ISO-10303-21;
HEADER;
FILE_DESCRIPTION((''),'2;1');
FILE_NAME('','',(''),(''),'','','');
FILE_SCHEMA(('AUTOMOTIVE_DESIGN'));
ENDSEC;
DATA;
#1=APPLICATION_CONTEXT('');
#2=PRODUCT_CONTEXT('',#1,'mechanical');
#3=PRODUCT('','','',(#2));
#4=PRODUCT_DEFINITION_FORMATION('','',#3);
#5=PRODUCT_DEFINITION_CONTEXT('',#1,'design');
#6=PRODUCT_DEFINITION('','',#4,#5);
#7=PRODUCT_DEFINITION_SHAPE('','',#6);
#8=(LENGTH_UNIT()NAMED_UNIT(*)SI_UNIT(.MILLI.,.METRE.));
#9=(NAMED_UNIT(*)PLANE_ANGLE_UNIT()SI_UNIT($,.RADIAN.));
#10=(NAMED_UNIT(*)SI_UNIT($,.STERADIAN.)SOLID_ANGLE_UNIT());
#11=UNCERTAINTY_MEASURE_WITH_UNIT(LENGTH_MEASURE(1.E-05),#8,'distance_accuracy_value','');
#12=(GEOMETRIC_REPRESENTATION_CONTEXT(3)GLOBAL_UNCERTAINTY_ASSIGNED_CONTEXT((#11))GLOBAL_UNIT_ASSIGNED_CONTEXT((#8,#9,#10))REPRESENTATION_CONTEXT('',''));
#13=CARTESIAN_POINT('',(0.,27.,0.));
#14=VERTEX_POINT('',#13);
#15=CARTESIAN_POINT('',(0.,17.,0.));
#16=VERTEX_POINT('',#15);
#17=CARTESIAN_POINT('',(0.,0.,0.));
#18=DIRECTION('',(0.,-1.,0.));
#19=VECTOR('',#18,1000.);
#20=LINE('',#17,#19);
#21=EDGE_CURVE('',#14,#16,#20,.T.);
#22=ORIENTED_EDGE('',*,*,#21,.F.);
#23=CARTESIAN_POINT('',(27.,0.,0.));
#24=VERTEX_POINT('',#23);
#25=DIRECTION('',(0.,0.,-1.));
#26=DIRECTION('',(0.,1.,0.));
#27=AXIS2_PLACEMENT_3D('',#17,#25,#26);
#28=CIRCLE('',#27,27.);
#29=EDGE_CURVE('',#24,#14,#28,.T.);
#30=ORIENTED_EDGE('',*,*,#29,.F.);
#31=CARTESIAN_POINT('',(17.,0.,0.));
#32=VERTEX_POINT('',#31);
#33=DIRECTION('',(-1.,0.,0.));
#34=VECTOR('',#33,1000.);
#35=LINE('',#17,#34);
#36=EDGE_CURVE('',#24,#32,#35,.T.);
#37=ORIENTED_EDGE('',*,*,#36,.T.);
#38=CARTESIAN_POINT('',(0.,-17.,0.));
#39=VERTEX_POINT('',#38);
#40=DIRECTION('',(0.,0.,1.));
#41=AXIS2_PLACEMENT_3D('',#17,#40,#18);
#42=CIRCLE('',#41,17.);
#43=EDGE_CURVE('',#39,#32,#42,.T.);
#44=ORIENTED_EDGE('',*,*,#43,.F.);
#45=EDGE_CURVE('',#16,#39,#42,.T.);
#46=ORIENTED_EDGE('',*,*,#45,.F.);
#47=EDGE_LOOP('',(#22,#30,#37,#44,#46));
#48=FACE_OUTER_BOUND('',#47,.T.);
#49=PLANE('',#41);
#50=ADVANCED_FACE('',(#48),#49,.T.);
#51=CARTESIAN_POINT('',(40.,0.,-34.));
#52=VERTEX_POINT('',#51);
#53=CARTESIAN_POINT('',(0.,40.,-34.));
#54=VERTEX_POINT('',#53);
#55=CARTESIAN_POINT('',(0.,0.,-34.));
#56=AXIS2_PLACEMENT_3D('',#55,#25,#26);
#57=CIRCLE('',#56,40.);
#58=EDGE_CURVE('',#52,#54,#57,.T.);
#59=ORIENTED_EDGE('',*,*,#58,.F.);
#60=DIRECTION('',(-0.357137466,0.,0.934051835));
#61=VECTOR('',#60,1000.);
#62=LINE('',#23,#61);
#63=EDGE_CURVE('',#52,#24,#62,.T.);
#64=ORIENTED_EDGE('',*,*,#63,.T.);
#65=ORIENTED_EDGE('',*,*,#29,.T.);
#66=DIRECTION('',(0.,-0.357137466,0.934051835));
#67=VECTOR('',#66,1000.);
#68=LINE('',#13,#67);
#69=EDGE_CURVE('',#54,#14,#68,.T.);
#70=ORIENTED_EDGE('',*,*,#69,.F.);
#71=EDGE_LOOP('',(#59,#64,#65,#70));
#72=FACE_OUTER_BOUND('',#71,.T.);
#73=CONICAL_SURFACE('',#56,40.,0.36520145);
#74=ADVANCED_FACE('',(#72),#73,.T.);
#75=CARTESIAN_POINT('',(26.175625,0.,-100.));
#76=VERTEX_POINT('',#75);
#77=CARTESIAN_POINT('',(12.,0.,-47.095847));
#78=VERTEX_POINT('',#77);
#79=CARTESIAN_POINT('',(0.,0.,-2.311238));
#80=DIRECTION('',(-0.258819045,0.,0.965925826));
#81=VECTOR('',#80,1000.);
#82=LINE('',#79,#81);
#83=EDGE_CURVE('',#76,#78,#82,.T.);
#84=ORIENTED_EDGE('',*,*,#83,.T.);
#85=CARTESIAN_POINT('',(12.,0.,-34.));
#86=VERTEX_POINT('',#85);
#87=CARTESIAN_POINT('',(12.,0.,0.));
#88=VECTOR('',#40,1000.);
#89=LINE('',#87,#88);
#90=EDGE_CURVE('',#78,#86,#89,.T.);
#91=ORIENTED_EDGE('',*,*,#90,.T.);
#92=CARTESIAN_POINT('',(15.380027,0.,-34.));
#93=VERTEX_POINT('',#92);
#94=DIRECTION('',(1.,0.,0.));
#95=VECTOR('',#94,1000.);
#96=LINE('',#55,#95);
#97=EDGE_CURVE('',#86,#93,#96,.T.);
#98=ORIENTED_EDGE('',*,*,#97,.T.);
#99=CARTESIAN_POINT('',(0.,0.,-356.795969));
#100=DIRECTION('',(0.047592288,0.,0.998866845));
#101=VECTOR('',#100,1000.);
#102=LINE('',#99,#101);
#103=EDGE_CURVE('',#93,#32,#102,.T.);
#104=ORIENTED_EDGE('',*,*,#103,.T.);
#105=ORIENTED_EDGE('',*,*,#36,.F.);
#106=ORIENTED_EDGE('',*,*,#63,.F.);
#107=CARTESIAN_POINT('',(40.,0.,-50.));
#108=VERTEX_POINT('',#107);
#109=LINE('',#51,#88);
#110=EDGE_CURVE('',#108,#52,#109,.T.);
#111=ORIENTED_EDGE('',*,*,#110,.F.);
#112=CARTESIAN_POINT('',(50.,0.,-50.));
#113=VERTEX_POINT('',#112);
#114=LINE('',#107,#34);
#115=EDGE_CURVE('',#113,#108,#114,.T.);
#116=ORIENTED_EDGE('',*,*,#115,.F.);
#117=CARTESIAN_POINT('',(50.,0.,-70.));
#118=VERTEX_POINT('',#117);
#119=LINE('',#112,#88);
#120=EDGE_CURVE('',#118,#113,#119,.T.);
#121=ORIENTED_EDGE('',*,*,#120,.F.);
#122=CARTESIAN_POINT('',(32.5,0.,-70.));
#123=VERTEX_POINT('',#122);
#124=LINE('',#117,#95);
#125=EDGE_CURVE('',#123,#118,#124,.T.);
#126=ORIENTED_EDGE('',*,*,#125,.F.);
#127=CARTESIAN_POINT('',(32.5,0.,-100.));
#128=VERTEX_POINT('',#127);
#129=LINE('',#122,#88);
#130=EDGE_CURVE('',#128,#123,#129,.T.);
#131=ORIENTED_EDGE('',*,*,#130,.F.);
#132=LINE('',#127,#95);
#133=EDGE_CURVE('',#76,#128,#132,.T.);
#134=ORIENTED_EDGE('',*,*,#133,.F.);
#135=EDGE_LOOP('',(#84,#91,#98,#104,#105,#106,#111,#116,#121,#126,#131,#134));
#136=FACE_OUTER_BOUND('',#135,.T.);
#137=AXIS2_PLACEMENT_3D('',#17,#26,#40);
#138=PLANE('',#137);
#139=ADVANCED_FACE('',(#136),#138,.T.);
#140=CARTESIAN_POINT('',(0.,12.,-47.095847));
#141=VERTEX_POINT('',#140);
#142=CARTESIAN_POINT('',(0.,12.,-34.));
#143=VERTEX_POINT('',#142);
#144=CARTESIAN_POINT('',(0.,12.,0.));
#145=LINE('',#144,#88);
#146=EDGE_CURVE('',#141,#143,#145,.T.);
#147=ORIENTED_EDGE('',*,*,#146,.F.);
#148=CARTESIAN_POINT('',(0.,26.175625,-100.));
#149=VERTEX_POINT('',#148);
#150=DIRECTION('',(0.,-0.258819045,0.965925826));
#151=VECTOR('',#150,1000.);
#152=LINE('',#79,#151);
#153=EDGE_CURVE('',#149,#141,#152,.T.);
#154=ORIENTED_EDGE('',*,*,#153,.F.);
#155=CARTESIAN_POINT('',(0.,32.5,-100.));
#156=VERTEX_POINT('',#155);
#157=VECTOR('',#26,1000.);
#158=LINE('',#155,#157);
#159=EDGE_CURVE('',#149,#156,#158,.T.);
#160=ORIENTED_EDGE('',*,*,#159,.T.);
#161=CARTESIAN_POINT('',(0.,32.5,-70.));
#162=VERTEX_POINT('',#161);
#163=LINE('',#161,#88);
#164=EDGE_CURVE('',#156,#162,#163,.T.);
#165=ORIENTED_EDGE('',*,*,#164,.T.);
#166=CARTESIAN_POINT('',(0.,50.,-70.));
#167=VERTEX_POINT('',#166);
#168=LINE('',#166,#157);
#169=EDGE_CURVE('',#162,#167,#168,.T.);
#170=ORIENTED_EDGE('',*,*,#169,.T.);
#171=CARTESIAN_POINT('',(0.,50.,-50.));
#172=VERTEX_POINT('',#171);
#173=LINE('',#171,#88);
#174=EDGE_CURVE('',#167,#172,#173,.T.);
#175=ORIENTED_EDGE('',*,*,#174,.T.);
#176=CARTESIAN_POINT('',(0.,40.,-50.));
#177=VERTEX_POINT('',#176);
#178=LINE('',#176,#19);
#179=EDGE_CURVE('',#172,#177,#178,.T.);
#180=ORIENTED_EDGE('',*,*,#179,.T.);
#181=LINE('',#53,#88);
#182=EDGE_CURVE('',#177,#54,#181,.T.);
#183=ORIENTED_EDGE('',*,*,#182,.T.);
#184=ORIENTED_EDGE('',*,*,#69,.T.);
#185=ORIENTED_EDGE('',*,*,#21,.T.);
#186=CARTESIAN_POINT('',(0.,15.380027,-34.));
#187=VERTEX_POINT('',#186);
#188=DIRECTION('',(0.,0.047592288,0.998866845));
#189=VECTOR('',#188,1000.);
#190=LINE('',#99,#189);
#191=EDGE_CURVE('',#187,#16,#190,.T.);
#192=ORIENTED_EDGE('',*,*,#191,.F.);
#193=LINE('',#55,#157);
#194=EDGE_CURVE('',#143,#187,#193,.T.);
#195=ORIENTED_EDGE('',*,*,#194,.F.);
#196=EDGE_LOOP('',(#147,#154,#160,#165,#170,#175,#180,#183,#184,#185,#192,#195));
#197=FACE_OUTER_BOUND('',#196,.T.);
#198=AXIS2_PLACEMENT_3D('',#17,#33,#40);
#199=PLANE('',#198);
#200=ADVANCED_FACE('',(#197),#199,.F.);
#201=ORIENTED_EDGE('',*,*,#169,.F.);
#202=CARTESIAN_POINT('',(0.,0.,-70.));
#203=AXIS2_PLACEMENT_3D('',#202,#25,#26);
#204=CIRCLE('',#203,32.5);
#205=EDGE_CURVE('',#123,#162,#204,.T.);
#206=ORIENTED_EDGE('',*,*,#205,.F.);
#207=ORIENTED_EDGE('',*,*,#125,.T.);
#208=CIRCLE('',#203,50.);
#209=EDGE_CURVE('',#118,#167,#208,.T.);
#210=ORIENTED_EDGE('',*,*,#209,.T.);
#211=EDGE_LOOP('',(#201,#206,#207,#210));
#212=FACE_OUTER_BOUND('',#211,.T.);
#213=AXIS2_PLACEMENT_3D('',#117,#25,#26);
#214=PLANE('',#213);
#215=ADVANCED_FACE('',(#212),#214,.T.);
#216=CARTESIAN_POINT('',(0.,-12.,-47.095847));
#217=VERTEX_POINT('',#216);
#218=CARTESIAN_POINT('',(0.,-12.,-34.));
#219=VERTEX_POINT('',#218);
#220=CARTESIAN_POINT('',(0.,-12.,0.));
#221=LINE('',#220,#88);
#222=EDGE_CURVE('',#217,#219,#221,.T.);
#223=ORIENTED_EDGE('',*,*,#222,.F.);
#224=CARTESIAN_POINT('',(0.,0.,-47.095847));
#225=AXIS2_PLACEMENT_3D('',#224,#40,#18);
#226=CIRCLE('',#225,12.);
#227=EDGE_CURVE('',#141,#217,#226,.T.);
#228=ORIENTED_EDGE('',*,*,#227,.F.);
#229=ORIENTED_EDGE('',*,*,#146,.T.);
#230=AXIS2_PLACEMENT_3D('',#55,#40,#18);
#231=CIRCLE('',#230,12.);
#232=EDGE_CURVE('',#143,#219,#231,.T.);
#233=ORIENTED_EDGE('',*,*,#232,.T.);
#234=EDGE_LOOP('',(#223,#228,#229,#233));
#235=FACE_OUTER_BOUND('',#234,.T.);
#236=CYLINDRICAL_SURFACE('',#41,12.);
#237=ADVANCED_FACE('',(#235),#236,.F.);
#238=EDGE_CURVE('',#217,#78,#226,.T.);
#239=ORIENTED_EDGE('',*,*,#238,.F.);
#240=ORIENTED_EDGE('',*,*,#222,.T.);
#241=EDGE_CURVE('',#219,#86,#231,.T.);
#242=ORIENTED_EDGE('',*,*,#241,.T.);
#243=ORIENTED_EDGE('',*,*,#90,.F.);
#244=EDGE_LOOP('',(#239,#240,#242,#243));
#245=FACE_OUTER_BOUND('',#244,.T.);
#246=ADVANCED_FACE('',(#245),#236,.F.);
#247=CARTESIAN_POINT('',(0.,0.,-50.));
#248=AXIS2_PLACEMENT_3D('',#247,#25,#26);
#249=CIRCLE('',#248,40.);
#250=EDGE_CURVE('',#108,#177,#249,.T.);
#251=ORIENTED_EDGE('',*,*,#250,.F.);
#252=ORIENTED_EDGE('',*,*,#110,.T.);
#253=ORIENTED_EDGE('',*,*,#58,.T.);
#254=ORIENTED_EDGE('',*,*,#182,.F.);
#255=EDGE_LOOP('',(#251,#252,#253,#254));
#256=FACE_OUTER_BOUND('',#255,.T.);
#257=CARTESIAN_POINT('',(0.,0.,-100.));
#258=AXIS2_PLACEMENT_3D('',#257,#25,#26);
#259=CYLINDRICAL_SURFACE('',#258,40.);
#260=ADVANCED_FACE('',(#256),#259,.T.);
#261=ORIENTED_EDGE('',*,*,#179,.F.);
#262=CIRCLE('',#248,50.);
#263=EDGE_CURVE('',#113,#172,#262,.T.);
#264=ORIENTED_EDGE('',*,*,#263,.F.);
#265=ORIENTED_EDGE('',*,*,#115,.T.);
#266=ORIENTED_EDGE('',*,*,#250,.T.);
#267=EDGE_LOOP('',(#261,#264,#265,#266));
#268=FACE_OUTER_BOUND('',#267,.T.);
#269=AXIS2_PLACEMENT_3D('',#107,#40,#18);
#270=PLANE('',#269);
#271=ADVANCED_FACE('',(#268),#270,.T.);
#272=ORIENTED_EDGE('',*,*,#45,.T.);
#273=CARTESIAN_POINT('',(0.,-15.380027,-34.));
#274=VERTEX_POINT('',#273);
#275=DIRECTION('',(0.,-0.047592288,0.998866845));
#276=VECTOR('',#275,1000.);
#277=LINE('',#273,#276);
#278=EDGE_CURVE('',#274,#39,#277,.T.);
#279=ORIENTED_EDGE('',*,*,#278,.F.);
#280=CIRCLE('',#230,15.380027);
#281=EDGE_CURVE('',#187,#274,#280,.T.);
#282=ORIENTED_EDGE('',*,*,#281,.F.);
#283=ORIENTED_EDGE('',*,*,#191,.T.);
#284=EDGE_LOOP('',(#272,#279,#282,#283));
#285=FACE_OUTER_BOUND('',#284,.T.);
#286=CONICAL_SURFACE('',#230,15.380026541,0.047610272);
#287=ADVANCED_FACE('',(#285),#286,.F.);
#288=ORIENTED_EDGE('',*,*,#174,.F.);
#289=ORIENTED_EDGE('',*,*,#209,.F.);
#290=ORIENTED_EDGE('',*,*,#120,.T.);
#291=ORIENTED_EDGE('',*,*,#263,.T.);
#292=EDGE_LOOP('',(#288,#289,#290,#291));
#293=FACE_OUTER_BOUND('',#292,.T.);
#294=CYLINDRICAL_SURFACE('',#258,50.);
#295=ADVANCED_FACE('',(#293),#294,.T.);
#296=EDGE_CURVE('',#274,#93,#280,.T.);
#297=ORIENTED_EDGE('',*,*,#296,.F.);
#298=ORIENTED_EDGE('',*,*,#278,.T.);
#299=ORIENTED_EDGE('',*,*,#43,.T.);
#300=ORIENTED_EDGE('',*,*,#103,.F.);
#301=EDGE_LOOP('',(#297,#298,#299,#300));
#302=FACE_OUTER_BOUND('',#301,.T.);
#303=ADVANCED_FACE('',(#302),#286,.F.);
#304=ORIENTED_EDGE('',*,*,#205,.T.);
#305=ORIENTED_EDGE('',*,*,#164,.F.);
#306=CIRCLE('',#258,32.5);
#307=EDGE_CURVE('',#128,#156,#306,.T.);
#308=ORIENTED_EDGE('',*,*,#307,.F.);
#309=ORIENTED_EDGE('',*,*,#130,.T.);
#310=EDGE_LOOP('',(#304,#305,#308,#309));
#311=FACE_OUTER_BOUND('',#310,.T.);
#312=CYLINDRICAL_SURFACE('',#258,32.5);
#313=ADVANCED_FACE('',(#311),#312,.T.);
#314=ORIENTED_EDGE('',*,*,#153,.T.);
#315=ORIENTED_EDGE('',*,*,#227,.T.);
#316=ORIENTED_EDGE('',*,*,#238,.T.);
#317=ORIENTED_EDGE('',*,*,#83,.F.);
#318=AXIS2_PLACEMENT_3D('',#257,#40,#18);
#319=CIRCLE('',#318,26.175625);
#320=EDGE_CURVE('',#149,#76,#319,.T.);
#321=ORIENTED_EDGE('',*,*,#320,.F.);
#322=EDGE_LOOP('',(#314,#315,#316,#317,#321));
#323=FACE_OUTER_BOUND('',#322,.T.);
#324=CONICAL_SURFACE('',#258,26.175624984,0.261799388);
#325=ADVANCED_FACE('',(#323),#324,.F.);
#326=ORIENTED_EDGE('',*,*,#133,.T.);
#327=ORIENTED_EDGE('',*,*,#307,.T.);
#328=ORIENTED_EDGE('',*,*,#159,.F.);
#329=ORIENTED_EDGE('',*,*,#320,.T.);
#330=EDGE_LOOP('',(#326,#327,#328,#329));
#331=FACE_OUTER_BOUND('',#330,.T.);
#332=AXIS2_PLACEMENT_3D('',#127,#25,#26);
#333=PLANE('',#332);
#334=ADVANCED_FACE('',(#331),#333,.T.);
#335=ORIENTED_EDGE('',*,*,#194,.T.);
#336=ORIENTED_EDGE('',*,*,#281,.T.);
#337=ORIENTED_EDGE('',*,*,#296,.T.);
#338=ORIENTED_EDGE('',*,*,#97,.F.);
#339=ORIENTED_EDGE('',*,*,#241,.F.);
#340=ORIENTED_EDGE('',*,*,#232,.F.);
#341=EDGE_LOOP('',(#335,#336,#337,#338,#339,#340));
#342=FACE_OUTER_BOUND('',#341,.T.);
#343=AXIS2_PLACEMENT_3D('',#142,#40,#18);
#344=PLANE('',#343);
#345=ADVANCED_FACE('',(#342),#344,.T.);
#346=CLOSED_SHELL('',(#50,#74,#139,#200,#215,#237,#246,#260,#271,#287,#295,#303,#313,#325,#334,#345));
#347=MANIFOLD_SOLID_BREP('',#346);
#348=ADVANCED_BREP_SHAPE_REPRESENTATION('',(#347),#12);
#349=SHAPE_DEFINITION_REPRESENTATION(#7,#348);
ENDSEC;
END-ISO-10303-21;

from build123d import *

# Parameters (mm, degrees)
HUB_BODY_REVOLVE_270DEG_ANGLE = 270


with BuildPart() as part:
    # Hub Profile Sketch → Hub Body Revolve 270deg (revolve)
    with BuildSketch(Plane(origin=(0, 0, 0), x_dir=(0, 0, -1), z_dir=(1, 0, 0))):
        Polygon((0, 0), (0, 27), (34, 40), (50, 40), (50, 50), (70, 50), (70, 32.5), (100, 32.5), (100, 0), align=None)
    revolve(axis=Axis((0, 0, -100), (0, 0, 1)), revolution_arc=HUB_BODY_REVOLVE_270DEG_ANGLE)

    # Tapered Bore Profile Sketch → Stepped Tapered Bore Cut (revolve, cut)
    with BuildSketch(Plane(origin=(0, 0, 0), x_dir=(0, 0, -1), z_dir=(1, 0, 0))):
        Polygon((0, 0), (0, 17), (34, 15.380026541), (34, 12), (47.09584733, 12), (100, 26.175624984), (100, 0), align=None)
    revolve(axis=Axis((0, 0, 0), (0, 0, -1)), mode=Mode.SUBTRACT)


solid = part.part
